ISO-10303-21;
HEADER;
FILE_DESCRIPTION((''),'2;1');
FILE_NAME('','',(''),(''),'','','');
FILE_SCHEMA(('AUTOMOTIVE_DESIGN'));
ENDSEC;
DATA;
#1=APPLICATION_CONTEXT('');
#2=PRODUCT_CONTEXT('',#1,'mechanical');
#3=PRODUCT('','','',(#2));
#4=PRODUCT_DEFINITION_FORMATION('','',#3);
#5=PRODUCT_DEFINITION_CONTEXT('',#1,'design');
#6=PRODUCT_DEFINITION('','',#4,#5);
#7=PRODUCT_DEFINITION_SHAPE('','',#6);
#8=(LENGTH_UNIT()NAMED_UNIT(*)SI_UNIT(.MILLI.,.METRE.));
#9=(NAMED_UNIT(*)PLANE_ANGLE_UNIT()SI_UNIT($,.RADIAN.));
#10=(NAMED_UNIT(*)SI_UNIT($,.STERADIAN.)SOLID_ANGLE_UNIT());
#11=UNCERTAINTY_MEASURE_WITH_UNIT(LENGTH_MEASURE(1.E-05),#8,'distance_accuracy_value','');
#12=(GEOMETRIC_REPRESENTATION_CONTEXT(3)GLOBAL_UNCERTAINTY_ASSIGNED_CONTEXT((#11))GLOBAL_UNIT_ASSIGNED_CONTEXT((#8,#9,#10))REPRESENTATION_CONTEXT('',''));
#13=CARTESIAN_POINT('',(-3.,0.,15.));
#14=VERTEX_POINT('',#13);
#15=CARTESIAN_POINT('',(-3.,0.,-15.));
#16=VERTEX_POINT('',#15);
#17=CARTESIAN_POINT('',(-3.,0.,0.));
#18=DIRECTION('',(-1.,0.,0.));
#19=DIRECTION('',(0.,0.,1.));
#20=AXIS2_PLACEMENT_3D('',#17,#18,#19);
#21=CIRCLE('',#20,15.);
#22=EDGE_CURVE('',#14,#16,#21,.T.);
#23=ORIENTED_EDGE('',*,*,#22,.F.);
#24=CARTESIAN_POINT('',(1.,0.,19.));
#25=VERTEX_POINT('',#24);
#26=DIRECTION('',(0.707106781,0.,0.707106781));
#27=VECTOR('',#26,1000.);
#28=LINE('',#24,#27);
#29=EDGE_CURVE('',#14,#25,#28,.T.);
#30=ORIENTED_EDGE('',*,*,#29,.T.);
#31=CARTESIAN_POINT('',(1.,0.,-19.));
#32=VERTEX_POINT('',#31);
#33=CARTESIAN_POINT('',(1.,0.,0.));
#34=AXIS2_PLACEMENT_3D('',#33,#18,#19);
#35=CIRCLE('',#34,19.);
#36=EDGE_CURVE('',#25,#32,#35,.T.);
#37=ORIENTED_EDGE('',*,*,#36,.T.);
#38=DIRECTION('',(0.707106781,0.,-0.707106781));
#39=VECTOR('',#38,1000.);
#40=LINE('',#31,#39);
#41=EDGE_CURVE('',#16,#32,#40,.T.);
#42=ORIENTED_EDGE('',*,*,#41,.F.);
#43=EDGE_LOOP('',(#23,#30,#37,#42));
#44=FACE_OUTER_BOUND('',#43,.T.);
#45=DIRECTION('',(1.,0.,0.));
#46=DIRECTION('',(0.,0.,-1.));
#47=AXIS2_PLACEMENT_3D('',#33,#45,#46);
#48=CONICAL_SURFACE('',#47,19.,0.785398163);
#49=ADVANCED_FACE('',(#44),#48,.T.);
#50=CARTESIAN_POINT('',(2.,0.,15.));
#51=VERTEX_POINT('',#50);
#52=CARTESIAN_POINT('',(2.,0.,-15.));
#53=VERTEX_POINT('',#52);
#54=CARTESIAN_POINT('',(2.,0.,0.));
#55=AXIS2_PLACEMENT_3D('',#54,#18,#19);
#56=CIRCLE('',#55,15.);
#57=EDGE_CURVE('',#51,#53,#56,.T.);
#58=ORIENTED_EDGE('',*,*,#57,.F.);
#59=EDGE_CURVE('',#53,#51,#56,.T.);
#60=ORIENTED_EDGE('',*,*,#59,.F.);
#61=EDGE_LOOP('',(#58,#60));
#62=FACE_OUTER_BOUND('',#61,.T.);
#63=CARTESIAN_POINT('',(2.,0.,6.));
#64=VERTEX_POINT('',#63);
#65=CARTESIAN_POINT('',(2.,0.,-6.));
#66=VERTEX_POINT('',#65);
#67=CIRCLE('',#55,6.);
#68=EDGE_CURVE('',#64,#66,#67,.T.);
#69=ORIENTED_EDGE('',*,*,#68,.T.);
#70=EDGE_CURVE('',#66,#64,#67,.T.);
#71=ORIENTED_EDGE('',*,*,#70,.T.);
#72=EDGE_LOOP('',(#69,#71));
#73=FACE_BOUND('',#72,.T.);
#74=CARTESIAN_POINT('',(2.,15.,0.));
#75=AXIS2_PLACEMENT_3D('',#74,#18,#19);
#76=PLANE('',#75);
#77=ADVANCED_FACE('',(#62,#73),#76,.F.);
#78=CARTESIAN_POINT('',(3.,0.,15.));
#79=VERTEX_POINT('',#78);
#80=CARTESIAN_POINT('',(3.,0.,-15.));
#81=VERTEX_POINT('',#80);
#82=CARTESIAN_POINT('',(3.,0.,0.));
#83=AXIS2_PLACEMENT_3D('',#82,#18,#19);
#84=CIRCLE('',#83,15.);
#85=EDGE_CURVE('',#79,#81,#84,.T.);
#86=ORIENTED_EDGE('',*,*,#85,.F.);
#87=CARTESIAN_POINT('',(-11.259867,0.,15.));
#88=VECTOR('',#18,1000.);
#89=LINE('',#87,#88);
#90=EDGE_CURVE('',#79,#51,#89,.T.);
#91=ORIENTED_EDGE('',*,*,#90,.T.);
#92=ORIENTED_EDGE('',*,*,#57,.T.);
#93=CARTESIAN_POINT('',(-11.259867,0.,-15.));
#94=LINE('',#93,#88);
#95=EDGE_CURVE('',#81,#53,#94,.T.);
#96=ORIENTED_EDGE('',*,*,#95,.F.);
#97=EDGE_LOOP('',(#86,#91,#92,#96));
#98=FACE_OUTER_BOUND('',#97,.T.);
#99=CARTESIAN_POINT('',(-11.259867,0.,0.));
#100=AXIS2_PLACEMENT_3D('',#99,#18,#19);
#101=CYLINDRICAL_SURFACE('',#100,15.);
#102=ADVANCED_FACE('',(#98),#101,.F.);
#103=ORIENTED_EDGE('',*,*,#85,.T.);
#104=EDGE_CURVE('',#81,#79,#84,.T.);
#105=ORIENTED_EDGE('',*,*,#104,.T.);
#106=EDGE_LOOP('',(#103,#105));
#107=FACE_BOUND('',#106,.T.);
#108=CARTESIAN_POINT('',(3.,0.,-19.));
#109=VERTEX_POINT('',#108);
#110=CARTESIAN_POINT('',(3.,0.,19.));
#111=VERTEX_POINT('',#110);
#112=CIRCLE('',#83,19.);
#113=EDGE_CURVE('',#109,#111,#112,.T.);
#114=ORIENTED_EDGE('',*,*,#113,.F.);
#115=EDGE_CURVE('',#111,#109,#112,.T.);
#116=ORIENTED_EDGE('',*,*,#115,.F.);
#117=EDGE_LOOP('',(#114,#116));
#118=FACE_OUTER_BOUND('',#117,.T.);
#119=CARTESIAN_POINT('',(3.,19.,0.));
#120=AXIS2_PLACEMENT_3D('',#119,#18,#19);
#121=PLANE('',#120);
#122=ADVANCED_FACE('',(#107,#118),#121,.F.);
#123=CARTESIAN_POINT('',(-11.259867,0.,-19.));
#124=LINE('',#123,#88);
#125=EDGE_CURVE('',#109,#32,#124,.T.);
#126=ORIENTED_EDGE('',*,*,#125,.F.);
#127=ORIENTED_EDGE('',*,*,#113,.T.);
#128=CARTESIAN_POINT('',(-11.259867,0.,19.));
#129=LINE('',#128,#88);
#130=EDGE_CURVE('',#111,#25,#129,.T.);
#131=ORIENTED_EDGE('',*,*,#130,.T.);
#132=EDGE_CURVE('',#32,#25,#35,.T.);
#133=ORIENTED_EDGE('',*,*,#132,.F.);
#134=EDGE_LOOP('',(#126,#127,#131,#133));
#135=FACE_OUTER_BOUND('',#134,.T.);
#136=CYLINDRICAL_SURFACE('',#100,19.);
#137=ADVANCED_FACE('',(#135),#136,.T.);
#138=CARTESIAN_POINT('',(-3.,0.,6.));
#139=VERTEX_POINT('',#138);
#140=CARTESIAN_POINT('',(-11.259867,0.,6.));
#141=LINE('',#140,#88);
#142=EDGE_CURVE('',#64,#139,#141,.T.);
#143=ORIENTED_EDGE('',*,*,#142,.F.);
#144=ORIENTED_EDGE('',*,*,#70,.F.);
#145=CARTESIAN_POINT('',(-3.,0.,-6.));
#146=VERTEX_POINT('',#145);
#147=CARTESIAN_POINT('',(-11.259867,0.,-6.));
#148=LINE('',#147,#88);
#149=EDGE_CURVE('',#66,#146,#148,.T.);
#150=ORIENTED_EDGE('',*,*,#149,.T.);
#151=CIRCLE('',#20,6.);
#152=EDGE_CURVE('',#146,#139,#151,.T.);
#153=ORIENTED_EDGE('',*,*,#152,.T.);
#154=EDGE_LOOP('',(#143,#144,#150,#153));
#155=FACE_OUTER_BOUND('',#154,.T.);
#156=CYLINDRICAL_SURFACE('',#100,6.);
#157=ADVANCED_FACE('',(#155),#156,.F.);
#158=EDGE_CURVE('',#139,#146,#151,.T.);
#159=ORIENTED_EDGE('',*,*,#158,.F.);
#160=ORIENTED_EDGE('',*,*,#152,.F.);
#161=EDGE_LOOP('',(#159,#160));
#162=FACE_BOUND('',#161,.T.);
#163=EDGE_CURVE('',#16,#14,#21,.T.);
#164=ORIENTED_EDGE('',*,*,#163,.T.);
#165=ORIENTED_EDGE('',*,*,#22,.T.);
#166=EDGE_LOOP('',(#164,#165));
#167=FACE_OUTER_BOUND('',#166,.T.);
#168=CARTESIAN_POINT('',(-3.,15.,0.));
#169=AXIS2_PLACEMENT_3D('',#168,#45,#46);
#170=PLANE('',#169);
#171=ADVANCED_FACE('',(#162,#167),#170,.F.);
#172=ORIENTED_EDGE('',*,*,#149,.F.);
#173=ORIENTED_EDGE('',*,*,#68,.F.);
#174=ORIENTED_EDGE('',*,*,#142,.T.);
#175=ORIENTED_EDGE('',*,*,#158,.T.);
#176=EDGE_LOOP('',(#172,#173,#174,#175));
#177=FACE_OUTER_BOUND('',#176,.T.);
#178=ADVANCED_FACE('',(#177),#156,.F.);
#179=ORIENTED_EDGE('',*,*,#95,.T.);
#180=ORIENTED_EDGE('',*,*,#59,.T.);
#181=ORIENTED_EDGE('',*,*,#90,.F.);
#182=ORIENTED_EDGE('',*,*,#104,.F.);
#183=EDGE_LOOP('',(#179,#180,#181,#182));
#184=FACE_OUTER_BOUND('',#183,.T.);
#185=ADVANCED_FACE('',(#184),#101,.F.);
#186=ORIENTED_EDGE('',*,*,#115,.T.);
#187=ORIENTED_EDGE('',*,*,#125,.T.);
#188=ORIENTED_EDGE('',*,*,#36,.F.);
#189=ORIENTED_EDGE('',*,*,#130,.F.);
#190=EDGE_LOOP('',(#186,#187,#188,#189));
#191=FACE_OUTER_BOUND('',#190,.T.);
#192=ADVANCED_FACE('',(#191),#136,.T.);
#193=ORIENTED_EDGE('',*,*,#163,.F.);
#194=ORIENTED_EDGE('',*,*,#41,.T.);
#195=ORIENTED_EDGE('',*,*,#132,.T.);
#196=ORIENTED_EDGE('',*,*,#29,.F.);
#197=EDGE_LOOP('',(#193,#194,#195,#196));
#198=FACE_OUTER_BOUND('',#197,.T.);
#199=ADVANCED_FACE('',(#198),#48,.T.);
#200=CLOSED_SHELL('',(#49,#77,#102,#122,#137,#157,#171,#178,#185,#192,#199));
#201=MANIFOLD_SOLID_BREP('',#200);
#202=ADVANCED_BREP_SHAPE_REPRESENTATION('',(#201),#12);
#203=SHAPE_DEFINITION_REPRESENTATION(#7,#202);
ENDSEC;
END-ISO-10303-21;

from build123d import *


with BuildPart() as part:
    # Sketch1 → Revolve2 (revolve)
    with BuildSketch(Plane.XY, mode=Mode.PRIVATE) as revolve2_sk:
        Polygon((-3, 15), (-3, 6), (2, 6), (2, 15), (3, 15), (3, 19), (1, 19), align=None)
    revolve(revolve2_sk.sketch.rotate(Axis((-11.259866943, 0, 0), (1, 0, 0)), 90), axis=Axis((-11.259866943, 0, 0), (1, 0, 0)))


solid = part.part
